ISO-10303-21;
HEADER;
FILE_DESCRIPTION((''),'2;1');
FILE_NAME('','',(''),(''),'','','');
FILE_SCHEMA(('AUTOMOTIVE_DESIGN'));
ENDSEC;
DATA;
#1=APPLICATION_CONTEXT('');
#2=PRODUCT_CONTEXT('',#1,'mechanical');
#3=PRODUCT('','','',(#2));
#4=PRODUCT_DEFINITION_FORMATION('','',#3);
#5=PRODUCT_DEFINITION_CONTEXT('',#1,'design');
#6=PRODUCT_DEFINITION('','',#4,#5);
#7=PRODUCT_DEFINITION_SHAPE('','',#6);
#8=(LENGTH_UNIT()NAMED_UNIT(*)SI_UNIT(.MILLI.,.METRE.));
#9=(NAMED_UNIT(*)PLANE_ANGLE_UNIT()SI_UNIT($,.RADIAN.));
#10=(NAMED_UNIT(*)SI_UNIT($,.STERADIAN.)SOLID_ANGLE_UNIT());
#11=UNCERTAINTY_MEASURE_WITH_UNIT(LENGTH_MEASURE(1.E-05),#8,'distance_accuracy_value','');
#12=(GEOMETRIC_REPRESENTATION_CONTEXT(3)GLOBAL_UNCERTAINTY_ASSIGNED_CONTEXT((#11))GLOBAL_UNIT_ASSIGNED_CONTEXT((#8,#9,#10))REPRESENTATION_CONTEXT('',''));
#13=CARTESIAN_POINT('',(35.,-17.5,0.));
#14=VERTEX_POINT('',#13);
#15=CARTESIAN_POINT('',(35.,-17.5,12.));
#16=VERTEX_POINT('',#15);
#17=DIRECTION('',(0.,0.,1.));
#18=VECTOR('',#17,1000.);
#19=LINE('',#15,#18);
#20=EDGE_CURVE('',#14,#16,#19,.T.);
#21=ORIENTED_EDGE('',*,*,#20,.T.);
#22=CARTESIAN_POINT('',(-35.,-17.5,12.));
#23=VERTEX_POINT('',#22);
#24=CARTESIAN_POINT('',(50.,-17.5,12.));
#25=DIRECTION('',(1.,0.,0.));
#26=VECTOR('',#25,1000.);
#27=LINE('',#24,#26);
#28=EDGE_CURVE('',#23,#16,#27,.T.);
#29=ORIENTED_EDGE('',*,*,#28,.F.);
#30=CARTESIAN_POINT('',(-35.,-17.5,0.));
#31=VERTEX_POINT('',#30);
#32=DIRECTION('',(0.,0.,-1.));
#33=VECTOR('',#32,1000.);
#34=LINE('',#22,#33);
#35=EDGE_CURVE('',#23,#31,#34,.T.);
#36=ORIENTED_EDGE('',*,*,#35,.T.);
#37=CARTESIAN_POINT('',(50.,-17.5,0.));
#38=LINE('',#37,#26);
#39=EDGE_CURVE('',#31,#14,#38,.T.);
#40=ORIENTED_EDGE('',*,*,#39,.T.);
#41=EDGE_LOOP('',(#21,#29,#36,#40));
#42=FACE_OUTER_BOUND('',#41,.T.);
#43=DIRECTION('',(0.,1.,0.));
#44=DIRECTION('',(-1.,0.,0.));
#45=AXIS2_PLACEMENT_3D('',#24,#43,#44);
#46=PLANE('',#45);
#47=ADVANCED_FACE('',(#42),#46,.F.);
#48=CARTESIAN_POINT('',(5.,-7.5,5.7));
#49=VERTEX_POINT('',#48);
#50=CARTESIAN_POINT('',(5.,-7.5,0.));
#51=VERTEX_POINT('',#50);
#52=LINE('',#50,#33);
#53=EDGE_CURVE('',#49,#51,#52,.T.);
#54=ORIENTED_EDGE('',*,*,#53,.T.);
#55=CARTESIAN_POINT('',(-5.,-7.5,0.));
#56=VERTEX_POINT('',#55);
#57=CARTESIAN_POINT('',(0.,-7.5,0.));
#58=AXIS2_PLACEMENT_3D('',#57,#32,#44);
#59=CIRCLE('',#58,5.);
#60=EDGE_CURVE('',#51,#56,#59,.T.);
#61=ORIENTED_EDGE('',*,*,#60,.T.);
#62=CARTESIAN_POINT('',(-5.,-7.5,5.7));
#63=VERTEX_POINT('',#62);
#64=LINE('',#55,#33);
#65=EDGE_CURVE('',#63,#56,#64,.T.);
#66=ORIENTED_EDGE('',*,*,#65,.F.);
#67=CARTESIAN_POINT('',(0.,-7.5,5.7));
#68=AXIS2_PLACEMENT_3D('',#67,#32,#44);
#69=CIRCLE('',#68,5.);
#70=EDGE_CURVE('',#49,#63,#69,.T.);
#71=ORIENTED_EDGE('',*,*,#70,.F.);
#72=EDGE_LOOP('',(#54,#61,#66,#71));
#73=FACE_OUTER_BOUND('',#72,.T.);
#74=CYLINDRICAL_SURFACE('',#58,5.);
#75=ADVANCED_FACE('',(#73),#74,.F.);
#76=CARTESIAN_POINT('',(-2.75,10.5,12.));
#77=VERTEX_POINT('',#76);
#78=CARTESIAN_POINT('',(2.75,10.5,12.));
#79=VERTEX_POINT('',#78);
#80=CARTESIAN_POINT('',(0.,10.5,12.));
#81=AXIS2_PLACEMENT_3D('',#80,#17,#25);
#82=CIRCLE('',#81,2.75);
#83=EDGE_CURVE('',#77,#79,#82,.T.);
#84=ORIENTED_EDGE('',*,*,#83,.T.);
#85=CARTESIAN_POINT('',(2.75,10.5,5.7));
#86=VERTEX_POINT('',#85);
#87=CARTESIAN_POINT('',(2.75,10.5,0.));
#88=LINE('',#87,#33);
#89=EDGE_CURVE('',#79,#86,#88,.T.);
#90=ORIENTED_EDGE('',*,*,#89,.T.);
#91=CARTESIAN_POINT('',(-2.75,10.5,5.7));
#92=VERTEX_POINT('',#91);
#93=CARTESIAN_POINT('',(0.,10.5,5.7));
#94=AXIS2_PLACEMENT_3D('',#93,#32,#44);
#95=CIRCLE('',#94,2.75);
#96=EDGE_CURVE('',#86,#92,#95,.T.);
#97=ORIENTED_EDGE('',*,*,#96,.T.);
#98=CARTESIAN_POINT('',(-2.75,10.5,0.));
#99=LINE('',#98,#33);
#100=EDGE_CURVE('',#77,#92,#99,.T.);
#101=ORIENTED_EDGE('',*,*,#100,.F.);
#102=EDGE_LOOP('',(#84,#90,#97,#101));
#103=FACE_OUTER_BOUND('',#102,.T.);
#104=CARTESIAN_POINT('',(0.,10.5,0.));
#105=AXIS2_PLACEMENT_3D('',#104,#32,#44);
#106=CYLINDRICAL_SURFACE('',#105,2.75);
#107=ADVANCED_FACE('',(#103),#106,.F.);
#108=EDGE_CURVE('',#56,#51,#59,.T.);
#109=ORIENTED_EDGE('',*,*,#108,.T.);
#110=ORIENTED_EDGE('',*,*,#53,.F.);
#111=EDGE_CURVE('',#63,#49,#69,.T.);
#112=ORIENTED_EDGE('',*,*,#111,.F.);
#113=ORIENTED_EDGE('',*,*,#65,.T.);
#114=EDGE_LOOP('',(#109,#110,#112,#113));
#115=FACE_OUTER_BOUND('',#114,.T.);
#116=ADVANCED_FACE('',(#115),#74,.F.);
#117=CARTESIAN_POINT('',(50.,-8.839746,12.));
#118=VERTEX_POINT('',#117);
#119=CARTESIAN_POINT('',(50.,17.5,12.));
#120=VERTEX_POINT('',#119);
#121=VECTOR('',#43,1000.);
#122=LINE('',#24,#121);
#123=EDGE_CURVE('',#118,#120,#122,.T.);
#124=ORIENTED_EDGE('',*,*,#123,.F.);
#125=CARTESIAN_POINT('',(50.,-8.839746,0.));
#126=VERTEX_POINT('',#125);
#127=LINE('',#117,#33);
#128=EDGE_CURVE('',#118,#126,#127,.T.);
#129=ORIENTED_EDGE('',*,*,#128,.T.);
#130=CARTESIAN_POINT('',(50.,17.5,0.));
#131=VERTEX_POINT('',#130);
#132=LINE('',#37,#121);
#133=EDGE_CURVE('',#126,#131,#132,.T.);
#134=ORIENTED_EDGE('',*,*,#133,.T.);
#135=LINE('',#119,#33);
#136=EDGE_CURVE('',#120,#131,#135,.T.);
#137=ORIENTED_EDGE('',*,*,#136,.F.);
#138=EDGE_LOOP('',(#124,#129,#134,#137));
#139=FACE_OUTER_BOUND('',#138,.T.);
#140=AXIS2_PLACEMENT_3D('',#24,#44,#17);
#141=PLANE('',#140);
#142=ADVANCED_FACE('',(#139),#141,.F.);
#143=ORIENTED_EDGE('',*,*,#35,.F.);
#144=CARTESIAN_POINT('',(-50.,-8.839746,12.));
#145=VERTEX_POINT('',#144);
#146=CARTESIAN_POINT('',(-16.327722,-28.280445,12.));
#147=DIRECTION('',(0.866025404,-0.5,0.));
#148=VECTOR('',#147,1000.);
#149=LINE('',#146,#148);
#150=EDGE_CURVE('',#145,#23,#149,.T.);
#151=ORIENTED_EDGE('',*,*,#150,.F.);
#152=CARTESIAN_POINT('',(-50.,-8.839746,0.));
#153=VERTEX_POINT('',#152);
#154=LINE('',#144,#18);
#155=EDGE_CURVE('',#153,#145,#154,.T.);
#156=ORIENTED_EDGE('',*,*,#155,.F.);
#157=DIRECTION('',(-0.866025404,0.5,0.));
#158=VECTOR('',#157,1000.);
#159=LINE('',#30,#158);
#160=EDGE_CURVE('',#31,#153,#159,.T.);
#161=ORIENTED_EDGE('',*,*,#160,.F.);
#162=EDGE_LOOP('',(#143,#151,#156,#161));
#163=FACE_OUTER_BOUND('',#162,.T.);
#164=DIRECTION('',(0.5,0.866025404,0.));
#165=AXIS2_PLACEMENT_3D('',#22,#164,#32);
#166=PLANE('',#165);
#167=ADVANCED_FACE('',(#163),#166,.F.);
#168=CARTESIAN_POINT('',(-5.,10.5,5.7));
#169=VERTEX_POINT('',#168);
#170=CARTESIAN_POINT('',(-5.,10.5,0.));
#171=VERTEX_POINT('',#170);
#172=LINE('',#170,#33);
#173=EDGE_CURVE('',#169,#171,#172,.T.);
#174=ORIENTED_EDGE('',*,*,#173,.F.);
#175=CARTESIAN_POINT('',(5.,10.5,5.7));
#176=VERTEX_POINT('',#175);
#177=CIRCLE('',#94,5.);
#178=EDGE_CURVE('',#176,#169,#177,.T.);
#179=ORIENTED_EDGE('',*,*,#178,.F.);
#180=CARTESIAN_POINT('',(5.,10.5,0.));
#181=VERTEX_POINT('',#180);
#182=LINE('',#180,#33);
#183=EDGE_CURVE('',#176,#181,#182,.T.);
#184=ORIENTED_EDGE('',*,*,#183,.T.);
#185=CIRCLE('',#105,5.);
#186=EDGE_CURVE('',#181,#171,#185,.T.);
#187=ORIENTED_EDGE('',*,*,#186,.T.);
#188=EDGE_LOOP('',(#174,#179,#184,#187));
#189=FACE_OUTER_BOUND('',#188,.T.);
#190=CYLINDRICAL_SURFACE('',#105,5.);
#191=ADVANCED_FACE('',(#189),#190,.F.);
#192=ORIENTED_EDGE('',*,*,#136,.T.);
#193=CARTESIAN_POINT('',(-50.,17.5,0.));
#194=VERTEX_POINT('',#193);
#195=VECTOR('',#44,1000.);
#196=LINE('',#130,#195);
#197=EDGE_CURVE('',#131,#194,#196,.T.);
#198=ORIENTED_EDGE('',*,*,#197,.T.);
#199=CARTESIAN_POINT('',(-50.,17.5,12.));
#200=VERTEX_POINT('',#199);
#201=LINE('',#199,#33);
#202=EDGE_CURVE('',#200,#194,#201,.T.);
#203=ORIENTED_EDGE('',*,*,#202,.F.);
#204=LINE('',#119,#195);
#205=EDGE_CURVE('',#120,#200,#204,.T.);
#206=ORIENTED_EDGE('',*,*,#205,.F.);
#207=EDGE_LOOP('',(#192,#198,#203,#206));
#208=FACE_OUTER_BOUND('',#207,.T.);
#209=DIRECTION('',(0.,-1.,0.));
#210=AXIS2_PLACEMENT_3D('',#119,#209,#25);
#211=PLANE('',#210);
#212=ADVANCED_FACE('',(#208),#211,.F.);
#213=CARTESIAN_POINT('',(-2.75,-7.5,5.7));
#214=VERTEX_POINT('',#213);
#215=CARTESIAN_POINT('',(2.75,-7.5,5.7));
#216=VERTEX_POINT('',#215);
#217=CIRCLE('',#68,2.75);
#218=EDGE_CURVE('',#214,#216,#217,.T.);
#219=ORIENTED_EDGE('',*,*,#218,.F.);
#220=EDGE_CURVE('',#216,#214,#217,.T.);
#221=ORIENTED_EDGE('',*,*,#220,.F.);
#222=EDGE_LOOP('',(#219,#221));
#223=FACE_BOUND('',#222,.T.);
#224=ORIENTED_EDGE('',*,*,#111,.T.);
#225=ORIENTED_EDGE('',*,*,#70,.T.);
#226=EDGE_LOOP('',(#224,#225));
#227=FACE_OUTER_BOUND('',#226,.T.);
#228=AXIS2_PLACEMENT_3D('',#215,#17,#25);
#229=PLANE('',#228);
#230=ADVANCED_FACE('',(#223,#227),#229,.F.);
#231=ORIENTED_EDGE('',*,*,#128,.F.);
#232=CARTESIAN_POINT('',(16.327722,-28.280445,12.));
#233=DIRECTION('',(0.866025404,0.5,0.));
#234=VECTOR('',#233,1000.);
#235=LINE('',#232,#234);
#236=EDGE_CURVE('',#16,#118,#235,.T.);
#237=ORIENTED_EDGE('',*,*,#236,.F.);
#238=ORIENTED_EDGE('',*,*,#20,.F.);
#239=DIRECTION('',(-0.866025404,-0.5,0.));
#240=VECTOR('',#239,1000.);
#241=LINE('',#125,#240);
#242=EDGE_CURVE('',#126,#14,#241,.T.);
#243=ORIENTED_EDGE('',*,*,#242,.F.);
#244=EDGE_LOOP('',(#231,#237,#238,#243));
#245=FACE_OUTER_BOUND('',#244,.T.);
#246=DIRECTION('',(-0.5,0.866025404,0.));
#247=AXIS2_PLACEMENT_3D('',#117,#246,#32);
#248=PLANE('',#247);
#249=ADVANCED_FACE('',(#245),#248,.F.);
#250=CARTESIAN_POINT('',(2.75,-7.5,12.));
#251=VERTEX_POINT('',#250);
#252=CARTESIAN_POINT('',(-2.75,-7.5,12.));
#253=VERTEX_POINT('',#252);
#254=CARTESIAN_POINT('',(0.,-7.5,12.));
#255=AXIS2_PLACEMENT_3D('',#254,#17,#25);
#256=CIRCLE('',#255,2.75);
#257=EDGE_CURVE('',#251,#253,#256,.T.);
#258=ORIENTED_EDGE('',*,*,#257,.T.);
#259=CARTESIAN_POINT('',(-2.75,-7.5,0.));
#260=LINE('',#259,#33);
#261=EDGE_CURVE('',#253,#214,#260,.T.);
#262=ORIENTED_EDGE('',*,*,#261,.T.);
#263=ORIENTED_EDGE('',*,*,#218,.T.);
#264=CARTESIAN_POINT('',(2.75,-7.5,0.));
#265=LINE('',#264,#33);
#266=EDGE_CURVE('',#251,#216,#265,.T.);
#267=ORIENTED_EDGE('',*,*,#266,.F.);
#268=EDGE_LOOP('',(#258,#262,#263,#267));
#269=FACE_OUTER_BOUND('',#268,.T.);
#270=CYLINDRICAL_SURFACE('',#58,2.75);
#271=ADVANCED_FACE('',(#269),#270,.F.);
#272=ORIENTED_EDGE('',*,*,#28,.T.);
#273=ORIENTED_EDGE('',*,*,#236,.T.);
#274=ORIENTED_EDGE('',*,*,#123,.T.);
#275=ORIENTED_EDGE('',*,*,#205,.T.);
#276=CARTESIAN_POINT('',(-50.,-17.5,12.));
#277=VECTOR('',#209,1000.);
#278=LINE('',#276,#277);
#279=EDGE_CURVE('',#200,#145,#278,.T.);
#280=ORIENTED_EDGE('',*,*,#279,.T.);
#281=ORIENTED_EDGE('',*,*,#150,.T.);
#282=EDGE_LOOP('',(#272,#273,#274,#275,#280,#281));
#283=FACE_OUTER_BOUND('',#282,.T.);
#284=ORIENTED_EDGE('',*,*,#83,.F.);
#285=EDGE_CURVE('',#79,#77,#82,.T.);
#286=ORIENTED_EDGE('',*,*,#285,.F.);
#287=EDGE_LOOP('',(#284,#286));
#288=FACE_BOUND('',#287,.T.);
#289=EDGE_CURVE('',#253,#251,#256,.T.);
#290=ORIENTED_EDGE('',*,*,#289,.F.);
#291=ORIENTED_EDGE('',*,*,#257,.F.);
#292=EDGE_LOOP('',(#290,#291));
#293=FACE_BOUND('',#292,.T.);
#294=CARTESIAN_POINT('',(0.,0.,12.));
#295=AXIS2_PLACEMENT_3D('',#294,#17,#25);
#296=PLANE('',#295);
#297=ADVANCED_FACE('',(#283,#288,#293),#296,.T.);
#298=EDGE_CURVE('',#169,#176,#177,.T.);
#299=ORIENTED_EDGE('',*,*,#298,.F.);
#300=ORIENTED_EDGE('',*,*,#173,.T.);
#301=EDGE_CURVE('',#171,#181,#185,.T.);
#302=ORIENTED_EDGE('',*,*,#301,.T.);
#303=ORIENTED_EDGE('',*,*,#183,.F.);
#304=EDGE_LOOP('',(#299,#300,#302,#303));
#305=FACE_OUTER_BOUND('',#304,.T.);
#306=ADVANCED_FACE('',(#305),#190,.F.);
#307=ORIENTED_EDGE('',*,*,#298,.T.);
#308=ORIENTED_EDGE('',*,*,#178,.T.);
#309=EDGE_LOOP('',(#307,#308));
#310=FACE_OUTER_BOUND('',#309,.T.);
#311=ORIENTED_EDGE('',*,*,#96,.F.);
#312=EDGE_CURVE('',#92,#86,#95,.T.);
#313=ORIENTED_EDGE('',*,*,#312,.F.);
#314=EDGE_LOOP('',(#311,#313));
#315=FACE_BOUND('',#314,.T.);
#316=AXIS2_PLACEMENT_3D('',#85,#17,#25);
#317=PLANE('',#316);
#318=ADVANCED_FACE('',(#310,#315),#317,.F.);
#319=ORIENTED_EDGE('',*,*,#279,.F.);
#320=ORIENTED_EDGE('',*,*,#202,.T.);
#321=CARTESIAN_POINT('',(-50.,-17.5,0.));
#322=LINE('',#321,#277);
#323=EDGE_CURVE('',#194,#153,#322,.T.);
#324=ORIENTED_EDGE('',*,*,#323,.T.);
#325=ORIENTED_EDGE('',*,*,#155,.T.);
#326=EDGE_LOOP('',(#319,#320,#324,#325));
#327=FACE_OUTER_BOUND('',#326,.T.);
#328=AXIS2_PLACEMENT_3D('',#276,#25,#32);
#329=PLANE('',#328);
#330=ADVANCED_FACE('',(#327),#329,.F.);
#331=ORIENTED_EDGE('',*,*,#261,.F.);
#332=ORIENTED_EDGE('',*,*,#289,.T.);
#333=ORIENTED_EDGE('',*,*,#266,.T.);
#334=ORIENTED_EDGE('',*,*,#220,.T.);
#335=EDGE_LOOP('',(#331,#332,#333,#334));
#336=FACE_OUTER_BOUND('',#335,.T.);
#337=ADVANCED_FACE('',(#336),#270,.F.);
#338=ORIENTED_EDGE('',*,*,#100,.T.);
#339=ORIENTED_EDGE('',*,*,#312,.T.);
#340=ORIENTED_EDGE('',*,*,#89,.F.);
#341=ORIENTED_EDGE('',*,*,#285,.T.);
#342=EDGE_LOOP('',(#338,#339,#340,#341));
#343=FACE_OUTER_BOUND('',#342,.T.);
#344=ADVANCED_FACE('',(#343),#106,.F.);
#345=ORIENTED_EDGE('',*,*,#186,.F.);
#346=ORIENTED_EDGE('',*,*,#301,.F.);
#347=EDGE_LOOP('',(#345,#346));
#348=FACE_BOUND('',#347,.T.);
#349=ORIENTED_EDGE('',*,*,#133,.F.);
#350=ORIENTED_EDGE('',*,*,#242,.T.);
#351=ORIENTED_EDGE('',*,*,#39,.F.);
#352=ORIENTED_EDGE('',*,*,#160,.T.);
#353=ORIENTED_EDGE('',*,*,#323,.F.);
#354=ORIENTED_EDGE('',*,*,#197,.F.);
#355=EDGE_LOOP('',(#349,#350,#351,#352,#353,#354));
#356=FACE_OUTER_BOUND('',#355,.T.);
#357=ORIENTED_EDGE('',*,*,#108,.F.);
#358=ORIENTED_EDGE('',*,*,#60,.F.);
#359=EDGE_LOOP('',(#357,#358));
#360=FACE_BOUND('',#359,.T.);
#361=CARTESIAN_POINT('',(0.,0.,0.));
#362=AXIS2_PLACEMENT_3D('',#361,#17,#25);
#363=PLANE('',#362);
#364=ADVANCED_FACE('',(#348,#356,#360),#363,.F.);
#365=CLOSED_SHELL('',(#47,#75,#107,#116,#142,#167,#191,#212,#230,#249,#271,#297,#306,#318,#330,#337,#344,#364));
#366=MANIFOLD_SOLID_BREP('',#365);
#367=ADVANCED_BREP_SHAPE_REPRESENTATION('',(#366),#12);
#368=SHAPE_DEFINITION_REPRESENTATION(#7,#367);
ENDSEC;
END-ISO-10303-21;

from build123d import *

# Parameters (mm, degrees)
SKETCH_1_W                = 100
SKETCH_1_H                = 35
EXTRUDE_1_DEPTH           = 12
CHAMFER_1_SIZE            = 15
CHAMFER_1_SIZE2           = 8.660254038
HOLE_WIZARD_1_D           = 5.5
HOLE_WIZARD_1_CBORE_D     = 10
HOLE_WIZARD_1_CBORE_DEPTH = 5.7


with BuildPart() as part:
    # 草图1 → 凸台-拉伸1 (new body)
    with BuildSketch(Plane.XY):
        Rectangle(SKETCH_1_W, SKETCH_1_H)
    extrude(amount=EXTRUDE_1_DEPTH)

    # 倒角1
    chamfer_1_edges = [part.edges().sort_by_distance(p)[0] for p in [
        (50, -17.5, 6),
        (-50, -17.5, 6),
    ]]
    chamfer_1_side = [part.faces().sort_by_distance(p)[0] for p in [
        (0, -17.5, 6),
    ]]
    chamfer(chamfer_1_edges, length=CHAMFER_1_SIZE, length2=CHAMFER_1_SIZE2, reference=chamfer_1_side[0])

    # 打孔尺寸(%根据)内六角圆柱头螺钉的类型1 (through all)
    with Locations(Plane(origin=(0, 0, 0), x_dir=(-1, 0, 0), z_dir=(0, 0, -1))):
        with Locations((0, 10.5), (0, -7.5)):
            CounterBoreHole(HOLE_WIZARD_1_D / 2, HOLE_WIZARD_1_CBORE_D / 2, HOLE_WIZARD_1_CBORE_DEPTH)


solid = part.part
